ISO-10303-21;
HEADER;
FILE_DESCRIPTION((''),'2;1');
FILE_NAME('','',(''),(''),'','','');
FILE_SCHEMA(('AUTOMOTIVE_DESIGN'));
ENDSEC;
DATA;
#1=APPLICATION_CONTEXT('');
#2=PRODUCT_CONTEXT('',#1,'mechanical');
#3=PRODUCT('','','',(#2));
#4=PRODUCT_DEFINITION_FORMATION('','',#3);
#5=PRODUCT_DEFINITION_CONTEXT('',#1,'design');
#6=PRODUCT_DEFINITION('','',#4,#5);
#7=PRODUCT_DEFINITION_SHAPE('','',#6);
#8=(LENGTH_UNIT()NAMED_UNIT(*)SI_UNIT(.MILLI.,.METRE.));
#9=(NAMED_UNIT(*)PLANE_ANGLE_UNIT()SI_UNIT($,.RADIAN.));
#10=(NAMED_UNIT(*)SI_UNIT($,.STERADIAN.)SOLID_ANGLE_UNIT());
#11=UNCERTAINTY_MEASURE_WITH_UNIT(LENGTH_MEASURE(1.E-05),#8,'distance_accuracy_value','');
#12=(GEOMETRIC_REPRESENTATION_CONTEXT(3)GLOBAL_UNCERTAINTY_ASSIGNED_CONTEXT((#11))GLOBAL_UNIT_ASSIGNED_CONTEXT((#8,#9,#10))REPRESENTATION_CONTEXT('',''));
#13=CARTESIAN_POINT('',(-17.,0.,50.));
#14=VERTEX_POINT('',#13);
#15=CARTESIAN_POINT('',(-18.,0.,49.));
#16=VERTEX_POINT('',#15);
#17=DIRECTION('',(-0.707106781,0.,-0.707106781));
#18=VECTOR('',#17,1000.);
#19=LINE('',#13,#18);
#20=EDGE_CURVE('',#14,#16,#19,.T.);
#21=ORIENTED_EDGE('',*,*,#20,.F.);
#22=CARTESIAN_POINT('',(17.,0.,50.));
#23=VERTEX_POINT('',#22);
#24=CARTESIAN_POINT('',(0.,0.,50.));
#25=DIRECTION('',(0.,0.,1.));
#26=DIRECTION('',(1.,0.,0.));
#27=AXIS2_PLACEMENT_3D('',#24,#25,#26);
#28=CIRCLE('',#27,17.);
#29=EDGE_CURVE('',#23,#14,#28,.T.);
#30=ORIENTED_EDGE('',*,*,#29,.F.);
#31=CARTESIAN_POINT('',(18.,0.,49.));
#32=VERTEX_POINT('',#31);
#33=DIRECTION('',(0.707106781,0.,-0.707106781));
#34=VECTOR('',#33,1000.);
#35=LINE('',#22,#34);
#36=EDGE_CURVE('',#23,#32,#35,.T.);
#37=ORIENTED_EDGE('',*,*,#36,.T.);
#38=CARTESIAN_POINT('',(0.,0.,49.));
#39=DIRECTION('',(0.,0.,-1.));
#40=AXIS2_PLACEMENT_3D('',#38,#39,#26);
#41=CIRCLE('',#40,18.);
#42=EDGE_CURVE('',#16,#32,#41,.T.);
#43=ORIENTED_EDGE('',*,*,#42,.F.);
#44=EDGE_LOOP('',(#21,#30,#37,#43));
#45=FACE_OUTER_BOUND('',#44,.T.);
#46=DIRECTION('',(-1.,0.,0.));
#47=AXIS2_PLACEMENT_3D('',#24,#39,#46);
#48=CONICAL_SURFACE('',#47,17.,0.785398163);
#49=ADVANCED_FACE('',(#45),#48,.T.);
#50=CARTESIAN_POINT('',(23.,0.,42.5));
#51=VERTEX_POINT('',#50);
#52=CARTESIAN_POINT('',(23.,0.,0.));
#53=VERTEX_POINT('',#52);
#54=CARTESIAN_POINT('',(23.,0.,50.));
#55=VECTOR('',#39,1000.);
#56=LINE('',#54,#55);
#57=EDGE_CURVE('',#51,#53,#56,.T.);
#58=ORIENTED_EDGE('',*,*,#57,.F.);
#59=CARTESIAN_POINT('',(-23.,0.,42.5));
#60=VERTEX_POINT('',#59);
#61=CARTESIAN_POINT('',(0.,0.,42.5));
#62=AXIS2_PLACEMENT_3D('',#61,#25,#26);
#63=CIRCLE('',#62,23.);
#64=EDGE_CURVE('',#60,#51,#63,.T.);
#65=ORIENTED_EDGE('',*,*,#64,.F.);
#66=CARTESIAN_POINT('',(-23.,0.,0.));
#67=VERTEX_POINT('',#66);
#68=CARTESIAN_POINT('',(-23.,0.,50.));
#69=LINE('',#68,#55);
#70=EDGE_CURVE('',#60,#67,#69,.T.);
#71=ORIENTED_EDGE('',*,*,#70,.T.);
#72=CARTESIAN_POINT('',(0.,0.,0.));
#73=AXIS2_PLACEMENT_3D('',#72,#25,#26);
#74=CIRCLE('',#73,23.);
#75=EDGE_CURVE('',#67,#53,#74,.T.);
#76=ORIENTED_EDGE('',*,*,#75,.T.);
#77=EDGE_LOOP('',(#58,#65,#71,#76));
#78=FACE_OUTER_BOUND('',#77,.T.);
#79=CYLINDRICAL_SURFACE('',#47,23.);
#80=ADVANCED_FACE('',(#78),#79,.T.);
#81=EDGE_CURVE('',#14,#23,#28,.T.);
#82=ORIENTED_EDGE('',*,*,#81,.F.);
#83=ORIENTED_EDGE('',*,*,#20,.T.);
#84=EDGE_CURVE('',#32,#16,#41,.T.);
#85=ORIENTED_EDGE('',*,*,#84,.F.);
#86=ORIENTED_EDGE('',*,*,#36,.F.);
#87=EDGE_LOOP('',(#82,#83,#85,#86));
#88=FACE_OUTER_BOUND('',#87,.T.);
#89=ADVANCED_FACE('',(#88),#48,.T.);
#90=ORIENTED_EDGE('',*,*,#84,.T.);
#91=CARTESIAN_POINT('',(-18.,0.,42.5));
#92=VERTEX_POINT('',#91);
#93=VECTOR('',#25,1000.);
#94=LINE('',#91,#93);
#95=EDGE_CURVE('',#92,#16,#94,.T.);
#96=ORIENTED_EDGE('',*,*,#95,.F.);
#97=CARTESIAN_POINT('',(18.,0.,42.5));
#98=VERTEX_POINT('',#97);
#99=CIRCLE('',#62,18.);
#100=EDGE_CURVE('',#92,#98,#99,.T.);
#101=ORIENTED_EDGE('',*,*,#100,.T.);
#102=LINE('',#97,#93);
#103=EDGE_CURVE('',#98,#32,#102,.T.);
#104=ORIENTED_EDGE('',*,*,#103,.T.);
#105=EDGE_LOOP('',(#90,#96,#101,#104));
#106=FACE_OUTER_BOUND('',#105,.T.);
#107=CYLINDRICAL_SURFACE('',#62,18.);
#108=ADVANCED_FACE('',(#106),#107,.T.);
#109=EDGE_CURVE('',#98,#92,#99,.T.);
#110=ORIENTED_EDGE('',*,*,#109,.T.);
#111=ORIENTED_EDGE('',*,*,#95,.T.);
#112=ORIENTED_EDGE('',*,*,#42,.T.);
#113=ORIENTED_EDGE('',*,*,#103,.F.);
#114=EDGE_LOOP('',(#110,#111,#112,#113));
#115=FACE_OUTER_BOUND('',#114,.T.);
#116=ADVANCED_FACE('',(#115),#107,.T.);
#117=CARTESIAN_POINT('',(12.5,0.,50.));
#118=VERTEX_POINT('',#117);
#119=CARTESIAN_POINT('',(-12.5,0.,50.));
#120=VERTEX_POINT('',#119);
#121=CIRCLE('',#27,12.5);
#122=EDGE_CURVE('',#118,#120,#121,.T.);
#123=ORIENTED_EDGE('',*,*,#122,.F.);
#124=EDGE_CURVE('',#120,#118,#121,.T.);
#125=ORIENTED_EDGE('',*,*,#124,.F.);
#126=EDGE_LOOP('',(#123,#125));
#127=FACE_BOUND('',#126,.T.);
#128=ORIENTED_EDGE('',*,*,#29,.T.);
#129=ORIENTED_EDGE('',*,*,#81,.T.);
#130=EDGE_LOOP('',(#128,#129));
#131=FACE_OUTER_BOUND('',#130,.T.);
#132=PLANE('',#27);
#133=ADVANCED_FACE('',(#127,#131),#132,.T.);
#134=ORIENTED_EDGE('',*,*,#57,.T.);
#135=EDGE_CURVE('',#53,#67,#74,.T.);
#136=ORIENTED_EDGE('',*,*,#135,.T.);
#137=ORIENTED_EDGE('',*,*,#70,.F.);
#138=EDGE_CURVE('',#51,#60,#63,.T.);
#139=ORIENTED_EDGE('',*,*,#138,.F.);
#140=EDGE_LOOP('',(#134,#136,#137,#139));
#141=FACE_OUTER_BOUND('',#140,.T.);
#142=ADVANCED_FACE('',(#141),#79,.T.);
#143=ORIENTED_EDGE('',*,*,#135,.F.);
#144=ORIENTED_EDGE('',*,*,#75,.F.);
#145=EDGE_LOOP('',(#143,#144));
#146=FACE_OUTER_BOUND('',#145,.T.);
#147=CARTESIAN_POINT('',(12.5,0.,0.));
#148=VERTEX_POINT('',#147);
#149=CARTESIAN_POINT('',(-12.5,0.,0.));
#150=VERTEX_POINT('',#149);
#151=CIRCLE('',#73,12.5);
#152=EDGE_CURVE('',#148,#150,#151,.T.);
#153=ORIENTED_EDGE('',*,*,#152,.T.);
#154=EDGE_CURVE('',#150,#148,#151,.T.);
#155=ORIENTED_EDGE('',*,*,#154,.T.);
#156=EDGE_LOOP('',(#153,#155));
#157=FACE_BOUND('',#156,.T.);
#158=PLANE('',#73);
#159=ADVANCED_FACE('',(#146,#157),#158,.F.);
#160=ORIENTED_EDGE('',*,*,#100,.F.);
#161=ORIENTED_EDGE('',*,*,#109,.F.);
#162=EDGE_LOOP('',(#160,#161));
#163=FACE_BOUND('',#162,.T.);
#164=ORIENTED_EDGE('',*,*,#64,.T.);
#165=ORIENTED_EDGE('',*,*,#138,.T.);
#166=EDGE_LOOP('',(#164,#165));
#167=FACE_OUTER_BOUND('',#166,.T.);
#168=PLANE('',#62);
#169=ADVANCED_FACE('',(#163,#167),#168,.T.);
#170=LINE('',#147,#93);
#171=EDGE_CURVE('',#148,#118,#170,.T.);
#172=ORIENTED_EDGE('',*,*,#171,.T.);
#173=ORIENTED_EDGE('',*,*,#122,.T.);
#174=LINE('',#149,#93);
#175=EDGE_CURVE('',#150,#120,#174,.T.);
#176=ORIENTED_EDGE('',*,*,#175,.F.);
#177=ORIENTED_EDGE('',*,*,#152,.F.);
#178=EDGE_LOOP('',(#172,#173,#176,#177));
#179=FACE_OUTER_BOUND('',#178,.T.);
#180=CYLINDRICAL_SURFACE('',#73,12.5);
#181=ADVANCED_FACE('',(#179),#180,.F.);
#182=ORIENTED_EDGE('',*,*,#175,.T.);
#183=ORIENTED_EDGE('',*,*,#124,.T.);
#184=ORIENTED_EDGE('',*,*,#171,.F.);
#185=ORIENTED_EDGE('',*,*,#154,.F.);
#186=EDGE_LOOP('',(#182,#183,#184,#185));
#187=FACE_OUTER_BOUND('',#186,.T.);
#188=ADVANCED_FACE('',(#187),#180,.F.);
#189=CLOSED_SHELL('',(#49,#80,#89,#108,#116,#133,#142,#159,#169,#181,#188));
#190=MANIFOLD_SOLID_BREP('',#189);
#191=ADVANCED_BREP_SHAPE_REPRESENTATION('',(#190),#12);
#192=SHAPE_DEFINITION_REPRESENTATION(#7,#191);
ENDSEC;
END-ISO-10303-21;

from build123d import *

# Parameters (mm, degrees)
SKETCH1_R           = 23
BOSS_EXTRUDE1_DEPTH = 50
CUT_EXTRUDE1_START  = -7.5
SKETCH2_R           = 23
SKETCH2_R_2         = 18
CUT_EXTRUDE1_DEPTH  = 7.5
SKETCH3_R           = 12.5
CUT_EXTRUDE2_DEPTH  = 60.648973168
CHAMFER1_SIZE       = 1


with BuildPart() as part:
    # Sketch1 → Boss-Extrude1 (new body)
    with BuildSketch(Plane.XY):
        Circle(SKETCH1_R)
    extrude(amount=BOSS_EXTRUDE1_DEPTH)

    # Sketch2 → Cut-Extrude1 (cut)
    with BuildSketch(Plane.XY.offset(50).offset(CUT_EXTRUDE1_START)):
        Circle(SKETCH2_R)
        Circle(SKETCH2_R_2, mode=Mode.SUBTRACT)
    extrude(amount=CUT_EXTRUDE1_DEPTH, mode=Mode.SUBTRACT)

    # Sketch3 → Cut-Extrude2 (cut, through all)
    with BuildSketch(Plane.XY.offset(50)):
        Circle(SKETCH3_R)
    extrude(amount=-CUT_EXTRUDE2_DEPTH, mode=Mode.SUBTRACT)

    # Chamfer1
    chamfer1_edges = [part.edges().sort_by_distance(p)[0] for p in [
        (-18, 0, 50),
    ]]
    chamfer(chamfer1_edges, length=CHAMFER1_SIZE)


solid = part.part
